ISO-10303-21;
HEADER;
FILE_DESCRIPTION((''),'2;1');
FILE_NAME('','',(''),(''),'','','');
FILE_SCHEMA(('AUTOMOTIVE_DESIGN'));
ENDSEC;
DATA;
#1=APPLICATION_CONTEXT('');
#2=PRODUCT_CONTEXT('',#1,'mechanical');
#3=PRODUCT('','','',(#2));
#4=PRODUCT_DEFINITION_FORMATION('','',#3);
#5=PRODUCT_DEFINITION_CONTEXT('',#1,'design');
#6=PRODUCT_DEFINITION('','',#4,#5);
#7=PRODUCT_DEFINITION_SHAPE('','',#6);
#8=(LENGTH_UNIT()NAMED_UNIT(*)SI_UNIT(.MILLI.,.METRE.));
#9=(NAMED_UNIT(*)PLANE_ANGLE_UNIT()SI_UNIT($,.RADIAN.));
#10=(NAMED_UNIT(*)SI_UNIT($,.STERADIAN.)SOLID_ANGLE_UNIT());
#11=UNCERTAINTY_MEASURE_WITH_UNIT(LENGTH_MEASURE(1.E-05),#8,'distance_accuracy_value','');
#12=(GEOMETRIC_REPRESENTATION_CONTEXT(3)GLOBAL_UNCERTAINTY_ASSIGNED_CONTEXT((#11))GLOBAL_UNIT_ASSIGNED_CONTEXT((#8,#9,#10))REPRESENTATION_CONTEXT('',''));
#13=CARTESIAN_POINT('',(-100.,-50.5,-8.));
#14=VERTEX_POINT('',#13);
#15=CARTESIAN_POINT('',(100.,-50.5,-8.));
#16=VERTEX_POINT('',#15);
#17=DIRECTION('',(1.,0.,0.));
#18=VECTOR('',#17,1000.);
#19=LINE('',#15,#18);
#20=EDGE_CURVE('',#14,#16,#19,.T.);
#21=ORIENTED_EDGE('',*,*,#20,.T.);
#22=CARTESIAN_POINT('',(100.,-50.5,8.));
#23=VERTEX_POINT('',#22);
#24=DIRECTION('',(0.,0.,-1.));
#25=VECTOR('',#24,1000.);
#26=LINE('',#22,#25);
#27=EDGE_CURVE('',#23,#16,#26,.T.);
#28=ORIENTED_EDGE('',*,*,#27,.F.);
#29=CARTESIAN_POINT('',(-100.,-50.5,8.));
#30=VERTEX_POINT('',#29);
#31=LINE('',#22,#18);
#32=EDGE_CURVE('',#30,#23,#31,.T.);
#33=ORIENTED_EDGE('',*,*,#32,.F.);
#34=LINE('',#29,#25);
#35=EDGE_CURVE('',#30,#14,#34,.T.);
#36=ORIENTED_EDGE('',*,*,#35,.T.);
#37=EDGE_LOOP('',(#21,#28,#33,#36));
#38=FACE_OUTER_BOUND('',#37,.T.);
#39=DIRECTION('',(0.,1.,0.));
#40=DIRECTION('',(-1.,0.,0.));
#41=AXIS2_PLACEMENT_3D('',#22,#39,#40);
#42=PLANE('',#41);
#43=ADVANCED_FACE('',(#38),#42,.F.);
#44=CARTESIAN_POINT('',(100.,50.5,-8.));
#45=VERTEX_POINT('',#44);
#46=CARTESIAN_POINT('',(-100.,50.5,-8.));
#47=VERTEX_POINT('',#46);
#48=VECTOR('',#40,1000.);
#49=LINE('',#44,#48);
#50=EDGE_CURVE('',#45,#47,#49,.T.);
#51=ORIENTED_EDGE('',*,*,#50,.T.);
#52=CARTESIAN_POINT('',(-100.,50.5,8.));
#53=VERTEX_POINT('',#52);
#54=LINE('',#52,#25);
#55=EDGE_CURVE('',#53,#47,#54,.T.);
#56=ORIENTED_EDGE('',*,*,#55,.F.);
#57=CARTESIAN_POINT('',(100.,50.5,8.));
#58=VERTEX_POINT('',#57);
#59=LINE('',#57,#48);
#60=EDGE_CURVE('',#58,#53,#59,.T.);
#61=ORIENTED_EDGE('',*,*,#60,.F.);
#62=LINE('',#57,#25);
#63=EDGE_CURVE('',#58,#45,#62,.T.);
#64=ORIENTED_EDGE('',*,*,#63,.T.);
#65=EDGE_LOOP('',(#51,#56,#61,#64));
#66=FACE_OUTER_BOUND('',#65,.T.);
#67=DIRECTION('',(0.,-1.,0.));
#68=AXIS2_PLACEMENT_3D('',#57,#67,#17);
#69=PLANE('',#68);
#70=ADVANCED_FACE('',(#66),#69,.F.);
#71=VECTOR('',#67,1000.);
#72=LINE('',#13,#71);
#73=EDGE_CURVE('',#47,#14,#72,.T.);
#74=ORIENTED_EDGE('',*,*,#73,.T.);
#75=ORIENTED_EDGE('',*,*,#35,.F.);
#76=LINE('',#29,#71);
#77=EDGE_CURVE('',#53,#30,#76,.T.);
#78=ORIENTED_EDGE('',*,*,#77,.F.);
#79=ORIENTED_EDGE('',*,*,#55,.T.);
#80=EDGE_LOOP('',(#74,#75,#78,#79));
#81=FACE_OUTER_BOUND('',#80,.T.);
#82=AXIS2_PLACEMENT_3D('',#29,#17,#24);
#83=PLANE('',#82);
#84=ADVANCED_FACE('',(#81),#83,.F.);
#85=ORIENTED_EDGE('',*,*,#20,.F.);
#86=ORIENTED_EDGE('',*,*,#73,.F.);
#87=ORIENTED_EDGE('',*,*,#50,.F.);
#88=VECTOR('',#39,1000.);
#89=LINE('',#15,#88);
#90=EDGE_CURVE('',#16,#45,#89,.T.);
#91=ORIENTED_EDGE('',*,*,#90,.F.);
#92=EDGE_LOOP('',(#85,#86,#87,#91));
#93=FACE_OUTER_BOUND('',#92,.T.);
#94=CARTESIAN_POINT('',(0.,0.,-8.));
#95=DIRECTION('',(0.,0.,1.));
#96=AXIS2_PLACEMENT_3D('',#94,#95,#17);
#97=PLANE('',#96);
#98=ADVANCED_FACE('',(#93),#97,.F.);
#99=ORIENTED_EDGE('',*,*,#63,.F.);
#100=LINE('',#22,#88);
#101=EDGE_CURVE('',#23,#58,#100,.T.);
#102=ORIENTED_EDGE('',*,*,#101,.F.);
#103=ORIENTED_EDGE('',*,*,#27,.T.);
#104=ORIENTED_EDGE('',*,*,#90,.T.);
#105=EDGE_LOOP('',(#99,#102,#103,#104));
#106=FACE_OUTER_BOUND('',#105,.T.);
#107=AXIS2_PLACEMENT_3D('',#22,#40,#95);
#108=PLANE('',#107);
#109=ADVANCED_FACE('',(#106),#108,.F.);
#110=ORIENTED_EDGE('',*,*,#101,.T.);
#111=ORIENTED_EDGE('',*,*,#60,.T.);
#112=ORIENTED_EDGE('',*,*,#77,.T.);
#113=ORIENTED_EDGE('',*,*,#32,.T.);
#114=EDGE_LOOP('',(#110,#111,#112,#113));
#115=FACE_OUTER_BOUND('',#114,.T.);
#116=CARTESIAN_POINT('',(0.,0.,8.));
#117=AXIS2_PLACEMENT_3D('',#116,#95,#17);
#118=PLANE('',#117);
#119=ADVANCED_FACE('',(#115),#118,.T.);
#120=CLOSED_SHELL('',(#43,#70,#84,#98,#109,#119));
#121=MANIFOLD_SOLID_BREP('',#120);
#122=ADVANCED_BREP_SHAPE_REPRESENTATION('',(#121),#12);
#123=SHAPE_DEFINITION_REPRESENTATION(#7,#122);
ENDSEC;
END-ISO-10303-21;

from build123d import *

# Parameters (mm, degrees)
SKETCH1_W           = 200
SKETCH1_H           = 101
BOSS_EXTRUDE1_DEPTH = 8


with BuildPart() as part:
    # Sketch1 → Boss-Extrude1 (new, symmetric)
    with BuildSketch(Plane.XY):
        Rectangle(SKETCH1_W, SKETCH1_H)
    extrude(amount=BOSS_EXTRUDE1_DEPTH, both=True)


solid = part.part
